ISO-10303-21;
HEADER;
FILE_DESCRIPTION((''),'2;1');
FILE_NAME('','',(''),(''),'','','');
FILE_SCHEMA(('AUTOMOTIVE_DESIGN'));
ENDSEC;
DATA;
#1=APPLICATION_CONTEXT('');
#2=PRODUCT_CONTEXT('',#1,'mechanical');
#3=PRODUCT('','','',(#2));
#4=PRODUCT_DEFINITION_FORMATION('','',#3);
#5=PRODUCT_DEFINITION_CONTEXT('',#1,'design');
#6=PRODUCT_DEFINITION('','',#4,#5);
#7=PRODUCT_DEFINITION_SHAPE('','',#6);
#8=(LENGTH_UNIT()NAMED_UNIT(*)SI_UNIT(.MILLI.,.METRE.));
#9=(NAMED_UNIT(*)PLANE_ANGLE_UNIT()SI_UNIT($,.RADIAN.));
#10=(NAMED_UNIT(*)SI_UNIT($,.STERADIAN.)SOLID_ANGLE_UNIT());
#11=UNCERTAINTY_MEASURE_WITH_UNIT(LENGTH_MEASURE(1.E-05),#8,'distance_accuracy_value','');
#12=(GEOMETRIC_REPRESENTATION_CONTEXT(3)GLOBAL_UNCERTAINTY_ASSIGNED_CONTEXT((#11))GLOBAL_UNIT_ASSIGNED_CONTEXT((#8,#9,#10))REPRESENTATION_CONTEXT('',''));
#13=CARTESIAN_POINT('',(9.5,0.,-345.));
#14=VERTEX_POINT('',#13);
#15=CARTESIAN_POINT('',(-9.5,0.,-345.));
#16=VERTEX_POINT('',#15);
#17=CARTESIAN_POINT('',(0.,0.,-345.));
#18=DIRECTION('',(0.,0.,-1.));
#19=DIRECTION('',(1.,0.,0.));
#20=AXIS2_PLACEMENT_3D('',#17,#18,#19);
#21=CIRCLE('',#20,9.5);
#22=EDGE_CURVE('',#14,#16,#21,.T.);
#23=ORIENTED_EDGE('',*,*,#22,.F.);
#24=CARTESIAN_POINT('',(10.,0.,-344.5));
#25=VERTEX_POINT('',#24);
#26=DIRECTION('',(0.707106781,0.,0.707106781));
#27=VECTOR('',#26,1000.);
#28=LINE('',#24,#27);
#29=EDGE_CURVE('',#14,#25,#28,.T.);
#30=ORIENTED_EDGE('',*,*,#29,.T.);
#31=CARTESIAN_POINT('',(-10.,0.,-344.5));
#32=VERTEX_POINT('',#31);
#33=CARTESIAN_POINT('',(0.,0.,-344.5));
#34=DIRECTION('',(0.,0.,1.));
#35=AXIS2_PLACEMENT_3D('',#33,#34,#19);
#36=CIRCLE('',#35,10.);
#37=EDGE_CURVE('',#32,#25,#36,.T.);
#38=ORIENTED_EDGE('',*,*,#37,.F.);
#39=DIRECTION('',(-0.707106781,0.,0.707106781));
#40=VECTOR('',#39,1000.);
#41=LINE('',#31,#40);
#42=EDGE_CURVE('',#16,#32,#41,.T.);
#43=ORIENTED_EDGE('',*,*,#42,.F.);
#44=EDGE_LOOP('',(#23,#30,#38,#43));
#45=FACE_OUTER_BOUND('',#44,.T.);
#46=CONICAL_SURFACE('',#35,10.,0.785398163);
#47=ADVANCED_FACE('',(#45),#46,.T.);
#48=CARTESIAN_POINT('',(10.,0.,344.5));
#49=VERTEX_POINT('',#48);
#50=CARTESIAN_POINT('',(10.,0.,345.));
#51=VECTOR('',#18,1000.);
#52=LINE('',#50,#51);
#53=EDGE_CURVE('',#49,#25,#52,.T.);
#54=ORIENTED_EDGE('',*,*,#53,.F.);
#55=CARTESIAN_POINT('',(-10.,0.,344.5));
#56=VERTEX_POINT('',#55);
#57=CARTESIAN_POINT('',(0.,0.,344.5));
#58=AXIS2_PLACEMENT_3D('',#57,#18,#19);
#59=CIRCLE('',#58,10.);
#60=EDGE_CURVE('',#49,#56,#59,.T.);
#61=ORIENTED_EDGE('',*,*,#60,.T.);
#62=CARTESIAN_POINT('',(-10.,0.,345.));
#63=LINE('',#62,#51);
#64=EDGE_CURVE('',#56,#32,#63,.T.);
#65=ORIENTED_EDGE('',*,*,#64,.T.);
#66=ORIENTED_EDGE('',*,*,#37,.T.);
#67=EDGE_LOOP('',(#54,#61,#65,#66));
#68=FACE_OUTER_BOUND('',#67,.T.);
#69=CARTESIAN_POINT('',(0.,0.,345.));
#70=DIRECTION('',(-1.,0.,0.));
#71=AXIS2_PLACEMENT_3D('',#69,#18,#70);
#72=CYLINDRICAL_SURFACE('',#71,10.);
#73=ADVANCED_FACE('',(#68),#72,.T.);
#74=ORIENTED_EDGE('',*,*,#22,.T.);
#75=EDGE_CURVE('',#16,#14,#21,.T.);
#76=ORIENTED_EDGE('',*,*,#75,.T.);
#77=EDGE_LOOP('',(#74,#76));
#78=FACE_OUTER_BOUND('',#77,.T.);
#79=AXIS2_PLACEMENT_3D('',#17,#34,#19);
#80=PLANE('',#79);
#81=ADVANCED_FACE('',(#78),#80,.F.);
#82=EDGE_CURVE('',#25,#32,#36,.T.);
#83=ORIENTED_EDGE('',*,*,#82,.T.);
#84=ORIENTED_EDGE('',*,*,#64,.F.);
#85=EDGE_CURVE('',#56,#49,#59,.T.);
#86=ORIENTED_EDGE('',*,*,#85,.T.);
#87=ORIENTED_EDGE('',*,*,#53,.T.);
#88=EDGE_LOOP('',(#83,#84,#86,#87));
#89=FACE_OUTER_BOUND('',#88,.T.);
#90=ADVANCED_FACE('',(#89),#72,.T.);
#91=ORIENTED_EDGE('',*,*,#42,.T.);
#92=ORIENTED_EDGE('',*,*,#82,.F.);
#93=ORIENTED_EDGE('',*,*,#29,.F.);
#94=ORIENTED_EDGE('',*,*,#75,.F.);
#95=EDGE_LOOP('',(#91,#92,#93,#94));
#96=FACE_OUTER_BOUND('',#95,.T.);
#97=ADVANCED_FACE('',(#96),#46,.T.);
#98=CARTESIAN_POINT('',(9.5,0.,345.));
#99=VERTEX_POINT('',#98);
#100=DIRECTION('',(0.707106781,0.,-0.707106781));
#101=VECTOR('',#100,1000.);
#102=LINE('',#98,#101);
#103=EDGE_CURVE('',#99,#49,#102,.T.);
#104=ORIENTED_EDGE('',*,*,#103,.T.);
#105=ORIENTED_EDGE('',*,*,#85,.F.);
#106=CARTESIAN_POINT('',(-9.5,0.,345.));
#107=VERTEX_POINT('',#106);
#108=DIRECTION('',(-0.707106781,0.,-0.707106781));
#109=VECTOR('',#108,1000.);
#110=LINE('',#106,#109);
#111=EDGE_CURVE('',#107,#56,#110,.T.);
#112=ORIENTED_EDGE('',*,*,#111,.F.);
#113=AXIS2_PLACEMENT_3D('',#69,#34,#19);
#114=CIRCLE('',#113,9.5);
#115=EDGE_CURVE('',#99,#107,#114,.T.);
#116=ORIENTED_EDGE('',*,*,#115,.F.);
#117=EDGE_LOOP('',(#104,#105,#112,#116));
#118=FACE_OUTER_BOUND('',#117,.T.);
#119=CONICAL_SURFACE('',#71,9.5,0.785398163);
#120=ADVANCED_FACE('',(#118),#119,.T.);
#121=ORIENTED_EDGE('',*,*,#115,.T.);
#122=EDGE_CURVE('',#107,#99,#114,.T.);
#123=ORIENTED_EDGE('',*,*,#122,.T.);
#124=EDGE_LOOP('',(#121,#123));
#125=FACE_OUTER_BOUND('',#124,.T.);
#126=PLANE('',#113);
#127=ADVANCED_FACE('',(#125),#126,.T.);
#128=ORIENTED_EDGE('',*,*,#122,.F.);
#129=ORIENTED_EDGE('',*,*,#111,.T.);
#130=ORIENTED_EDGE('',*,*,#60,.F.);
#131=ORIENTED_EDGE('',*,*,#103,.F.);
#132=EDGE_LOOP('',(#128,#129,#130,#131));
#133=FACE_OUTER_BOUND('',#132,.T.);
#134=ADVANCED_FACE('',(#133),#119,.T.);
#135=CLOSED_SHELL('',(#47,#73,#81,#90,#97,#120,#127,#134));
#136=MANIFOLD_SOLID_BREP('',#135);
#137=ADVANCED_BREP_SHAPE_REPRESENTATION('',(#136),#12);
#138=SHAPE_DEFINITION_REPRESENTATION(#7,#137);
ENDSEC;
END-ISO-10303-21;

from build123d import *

# Parameters (mm, degrees)
SKETCH_1_R      = 10
EXTRUDE_1_DEPTH = 345
CHAMFER_1_SIZE  = 0.5


with BuildPart() as part:
    # 草图1 → 凸台-拉伸1 (new, symmetric)
    with BuildSketch(Plane.XY):
        with Locations(Location((0, 0, 0), (0, 0, 180))):
            Circle(SKETCH_1_R)
    extrude(amount=EXTRUDE_1_DEPTH, both=True)

    # 倒角1
    chamfer_1_edges = [part.edges().sort_by_distance(p)[0] for p in [
        (10, 0, -345),
        (10, 0, 345),
    ]]
    chamfer(chamfer_1_edges, length=CHAMFER_1_SIZE)


solid = part.part
